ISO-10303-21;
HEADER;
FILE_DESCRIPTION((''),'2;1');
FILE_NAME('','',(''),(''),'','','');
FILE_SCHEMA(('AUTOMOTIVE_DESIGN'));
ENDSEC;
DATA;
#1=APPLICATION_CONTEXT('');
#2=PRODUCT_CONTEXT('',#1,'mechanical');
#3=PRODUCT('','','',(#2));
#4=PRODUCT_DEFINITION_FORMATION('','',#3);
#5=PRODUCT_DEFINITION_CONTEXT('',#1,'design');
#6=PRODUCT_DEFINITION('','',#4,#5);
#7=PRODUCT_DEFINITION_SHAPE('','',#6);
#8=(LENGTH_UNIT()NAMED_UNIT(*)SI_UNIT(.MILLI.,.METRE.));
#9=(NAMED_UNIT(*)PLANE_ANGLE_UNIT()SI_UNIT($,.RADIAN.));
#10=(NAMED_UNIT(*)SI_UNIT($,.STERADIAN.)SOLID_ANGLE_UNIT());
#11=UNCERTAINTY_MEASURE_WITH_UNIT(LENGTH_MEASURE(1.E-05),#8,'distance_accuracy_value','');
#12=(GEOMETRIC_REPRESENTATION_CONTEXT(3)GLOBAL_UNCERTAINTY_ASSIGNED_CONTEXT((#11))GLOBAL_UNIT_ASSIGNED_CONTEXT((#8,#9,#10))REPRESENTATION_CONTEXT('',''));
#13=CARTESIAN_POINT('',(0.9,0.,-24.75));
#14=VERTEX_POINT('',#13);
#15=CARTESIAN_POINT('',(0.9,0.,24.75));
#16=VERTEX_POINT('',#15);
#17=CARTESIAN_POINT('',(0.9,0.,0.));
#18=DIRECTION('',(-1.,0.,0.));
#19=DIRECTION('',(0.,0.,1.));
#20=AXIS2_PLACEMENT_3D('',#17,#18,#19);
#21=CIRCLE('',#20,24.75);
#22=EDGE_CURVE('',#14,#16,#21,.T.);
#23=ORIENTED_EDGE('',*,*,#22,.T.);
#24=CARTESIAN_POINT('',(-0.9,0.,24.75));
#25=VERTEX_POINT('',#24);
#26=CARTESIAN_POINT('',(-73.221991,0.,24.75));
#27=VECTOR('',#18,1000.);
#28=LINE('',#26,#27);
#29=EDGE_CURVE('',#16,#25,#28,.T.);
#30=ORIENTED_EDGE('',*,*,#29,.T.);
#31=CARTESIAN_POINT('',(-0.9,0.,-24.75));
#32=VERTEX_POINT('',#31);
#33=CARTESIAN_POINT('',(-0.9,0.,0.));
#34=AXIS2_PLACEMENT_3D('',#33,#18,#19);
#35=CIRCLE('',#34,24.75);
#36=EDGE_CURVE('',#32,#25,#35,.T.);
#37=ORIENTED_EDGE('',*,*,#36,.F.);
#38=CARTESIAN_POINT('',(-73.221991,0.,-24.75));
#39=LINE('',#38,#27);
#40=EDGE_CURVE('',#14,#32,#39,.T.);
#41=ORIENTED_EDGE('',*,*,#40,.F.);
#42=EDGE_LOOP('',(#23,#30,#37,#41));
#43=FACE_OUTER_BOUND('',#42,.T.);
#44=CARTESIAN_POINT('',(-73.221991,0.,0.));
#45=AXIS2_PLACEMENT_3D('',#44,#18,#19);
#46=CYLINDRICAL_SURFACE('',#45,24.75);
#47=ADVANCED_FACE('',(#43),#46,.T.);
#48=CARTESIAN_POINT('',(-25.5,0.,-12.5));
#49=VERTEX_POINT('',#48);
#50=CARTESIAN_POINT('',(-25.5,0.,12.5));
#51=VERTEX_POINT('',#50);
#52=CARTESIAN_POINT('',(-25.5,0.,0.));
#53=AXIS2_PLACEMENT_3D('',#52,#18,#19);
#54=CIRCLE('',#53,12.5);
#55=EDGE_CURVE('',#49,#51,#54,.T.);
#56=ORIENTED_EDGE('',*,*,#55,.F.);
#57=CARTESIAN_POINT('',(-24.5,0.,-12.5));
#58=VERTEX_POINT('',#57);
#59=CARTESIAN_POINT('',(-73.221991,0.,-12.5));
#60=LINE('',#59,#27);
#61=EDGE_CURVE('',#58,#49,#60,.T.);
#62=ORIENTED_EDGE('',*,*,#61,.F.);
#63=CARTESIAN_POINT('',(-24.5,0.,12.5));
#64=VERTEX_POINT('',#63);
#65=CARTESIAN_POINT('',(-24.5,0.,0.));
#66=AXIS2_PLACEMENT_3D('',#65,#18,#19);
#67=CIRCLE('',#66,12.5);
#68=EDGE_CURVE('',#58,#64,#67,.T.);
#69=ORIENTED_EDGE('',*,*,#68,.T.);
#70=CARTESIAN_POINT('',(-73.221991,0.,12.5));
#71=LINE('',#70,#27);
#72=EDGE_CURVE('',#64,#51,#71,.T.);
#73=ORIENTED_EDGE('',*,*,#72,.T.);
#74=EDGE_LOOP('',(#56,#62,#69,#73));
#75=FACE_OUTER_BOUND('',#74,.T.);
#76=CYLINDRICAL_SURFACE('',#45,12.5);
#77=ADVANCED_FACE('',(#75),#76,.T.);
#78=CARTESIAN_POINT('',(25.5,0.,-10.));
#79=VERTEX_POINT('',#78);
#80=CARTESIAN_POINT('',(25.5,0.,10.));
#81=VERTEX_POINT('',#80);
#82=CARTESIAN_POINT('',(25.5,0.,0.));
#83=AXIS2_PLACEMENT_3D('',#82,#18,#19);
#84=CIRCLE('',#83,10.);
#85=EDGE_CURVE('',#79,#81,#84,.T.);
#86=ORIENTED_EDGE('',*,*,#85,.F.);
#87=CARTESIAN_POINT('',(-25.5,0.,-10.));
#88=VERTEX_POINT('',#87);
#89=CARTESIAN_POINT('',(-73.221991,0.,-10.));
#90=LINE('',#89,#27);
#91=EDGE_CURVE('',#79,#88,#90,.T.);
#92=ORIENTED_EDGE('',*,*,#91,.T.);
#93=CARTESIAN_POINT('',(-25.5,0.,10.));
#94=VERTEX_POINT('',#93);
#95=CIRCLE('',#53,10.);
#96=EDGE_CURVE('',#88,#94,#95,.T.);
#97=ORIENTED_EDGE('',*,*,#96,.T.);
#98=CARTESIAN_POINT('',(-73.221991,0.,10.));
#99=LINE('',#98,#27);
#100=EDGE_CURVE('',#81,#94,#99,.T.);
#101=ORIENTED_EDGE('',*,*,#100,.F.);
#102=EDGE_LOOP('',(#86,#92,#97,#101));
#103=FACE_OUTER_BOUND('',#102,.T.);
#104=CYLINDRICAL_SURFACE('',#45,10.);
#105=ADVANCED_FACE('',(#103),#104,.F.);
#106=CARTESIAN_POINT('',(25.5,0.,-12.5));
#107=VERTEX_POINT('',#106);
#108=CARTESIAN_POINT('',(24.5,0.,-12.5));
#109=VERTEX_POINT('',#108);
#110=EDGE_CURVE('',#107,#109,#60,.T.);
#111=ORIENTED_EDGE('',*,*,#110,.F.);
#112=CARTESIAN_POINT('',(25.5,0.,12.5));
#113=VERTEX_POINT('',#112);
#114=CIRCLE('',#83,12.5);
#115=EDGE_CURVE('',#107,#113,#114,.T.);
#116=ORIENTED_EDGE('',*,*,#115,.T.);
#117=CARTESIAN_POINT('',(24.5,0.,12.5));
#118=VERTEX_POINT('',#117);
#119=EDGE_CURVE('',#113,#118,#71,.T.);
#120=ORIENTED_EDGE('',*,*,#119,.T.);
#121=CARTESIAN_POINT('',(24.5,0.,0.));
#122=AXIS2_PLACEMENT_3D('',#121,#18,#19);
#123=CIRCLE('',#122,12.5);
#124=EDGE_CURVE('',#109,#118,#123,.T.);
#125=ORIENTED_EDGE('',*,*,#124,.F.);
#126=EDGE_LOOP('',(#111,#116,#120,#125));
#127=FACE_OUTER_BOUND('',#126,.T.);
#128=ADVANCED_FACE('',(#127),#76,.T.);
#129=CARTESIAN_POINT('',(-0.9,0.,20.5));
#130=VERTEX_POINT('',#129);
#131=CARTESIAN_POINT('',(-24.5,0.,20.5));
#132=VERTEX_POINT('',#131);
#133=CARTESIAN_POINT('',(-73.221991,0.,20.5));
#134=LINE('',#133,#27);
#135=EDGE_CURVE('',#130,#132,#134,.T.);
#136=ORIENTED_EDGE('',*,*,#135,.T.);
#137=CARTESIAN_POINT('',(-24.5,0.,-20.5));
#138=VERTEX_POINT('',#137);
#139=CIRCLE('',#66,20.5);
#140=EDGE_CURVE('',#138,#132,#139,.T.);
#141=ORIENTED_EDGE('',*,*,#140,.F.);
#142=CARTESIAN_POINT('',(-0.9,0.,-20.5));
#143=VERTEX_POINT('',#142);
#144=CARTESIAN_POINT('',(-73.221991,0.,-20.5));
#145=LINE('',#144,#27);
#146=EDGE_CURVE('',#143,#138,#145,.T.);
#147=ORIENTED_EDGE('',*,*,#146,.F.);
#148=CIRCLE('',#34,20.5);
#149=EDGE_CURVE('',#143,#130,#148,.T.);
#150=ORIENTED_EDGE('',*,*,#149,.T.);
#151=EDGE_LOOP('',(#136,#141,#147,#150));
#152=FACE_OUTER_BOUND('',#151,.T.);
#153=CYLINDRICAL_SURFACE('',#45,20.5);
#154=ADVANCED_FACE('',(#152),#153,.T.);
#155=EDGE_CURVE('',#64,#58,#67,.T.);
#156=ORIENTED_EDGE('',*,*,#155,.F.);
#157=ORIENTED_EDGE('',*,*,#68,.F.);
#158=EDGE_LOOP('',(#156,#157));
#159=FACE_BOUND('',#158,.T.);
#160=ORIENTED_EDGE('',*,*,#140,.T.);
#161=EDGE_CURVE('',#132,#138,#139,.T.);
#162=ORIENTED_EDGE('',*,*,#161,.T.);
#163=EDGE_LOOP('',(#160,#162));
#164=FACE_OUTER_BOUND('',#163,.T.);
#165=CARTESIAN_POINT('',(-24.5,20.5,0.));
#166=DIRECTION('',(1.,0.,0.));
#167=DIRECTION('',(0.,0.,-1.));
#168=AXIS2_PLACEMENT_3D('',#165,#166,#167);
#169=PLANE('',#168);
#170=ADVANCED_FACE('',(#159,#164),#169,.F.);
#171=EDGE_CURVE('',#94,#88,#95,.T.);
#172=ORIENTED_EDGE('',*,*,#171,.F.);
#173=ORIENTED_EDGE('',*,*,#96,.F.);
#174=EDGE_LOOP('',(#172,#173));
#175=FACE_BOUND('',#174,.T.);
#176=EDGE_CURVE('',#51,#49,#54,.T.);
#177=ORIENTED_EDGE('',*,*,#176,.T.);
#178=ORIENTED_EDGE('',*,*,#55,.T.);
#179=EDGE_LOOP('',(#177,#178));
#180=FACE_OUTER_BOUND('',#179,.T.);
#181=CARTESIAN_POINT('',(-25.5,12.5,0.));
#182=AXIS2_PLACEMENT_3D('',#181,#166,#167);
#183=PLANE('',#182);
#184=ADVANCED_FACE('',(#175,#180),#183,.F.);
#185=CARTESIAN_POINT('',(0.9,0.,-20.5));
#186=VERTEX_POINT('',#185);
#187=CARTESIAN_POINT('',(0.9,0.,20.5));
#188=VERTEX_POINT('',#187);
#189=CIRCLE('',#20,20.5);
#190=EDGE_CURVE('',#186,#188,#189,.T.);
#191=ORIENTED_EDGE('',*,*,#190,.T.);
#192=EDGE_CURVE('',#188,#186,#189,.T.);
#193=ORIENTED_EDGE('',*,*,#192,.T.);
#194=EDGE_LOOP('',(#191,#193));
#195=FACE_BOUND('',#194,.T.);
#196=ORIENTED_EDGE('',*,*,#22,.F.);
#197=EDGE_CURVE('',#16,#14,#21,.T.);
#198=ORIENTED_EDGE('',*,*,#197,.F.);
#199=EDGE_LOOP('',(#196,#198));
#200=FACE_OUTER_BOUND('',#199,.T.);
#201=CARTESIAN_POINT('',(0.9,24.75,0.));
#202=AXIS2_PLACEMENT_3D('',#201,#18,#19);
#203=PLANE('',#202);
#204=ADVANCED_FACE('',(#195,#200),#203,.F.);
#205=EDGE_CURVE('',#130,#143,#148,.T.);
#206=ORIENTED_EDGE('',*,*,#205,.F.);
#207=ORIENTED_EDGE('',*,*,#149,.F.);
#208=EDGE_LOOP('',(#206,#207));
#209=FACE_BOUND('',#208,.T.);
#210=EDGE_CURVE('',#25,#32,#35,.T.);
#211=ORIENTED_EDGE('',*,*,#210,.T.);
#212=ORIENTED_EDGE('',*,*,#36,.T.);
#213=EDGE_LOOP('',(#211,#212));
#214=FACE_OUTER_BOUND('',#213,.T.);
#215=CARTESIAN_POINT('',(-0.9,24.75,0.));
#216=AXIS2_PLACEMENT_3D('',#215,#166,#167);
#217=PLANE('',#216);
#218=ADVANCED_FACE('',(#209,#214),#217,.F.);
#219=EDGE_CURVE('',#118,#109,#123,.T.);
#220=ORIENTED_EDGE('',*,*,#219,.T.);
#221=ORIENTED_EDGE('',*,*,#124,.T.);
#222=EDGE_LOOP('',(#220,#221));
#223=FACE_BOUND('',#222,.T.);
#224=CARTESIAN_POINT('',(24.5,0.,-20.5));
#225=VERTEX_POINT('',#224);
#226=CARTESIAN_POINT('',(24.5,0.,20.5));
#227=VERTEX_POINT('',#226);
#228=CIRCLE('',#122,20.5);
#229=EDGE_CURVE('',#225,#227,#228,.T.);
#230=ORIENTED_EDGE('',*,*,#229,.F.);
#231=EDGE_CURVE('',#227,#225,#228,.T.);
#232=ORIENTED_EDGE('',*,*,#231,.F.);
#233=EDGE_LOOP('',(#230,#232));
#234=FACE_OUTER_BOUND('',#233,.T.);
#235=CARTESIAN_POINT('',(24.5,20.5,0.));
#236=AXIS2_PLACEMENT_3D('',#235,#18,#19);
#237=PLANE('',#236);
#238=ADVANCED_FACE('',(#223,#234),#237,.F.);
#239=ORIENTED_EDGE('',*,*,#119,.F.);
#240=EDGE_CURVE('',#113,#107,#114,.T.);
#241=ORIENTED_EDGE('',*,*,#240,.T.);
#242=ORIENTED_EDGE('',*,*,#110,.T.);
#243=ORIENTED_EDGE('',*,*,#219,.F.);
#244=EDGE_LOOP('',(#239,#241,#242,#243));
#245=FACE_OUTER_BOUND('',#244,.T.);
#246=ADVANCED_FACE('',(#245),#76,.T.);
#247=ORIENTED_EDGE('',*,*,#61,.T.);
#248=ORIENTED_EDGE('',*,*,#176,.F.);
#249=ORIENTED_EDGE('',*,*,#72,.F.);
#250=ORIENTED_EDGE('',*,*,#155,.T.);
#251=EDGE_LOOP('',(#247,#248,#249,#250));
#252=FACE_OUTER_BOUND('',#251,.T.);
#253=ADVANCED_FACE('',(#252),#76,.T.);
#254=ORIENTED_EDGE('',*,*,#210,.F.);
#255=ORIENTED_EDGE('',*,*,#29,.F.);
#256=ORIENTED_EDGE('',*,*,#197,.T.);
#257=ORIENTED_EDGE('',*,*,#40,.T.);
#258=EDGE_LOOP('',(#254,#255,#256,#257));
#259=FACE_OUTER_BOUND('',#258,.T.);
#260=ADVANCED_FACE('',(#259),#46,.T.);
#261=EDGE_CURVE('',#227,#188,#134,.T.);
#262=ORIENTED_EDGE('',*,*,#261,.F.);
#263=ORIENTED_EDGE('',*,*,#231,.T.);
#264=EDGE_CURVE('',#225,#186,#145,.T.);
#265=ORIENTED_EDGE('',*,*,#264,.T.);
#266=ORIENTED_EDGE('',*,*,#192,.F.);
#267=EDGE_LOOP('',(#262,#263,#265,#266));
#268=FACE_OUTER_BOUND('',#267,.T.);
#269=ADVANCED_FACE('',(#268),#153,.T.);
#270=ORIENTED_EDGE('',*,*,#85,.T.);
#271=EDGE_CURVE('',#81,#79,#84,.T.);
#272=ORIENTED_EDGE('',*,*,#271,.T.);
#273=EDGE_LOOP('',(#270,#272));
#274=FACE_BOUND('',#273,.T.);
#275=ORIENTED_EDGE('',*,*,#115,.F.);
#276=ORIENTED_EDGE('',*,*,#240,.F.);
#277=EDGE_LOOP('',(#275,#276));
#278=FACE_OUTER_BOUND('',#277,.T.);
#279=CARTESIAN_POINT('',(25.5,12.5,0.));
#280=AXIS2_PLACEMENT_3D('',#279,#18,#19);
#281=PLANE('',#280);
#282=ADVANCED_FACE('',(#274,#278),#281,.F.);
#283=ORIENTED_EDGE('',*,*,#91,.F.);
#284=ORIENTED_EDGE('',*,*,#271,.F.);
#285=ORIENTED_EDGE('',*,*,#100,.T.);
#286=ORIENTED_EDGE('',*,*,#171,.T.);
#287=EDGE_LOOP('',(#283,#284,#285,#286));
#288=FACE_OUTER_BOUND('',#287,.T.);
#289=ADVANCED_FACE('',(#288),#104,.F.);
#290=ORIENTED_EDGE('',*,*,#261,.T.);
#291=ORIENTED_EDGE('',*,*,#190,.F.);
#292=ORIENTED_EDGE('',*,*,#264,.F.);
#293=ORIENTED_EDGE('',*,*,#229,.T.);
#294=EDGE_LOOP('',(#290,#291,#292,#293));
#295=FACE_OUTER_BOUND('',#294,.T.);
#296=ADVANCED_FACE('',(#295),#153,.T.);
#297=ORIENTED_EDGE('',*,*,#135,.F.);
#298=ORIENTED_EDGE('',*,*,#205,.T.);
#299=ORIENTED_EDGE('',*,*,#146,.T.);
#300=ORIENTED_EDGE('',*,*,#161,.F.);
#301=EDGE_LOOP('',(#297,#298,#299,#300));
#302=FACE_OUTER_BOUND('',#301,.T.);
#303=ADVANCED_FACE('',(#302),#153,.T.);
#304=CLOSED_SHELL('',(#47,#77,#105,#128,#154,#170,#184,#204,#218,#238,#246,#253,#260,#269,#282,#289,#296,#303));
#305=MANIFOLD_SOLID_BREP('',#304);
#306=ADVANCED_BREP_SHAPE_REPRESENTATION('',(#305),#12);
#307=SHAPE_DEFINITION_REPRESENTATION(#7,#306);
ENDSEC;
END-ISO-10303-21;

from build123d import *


with BuildPart() as part:
    # 草图1 → 旋转1 (revolve)
    with BuildSketch(Plane.XY, mode=Mode.PRIVATE) as revolve_1_sk:
        Polygon((-0.9, 24.75), (0.9, 24.75), (0.9, 20.5), (24.5, 20.5), (24.5, 12.5), (25.5, 12.5), (25.5, 10), (-25.5, 10), (-25.5, 12.5), (-24.5, 12.5), (-24.5, 20.5), (-0.9, 20.5), align=None)
    revolve(revolve_1_sk.sketch.rotate(Axis((-73.221991318, 0, 0), (1, 0, 0)), 90), axis=Axis((-73.221991318, 0, 0), (1, 0, 0)))


solid = part.part
